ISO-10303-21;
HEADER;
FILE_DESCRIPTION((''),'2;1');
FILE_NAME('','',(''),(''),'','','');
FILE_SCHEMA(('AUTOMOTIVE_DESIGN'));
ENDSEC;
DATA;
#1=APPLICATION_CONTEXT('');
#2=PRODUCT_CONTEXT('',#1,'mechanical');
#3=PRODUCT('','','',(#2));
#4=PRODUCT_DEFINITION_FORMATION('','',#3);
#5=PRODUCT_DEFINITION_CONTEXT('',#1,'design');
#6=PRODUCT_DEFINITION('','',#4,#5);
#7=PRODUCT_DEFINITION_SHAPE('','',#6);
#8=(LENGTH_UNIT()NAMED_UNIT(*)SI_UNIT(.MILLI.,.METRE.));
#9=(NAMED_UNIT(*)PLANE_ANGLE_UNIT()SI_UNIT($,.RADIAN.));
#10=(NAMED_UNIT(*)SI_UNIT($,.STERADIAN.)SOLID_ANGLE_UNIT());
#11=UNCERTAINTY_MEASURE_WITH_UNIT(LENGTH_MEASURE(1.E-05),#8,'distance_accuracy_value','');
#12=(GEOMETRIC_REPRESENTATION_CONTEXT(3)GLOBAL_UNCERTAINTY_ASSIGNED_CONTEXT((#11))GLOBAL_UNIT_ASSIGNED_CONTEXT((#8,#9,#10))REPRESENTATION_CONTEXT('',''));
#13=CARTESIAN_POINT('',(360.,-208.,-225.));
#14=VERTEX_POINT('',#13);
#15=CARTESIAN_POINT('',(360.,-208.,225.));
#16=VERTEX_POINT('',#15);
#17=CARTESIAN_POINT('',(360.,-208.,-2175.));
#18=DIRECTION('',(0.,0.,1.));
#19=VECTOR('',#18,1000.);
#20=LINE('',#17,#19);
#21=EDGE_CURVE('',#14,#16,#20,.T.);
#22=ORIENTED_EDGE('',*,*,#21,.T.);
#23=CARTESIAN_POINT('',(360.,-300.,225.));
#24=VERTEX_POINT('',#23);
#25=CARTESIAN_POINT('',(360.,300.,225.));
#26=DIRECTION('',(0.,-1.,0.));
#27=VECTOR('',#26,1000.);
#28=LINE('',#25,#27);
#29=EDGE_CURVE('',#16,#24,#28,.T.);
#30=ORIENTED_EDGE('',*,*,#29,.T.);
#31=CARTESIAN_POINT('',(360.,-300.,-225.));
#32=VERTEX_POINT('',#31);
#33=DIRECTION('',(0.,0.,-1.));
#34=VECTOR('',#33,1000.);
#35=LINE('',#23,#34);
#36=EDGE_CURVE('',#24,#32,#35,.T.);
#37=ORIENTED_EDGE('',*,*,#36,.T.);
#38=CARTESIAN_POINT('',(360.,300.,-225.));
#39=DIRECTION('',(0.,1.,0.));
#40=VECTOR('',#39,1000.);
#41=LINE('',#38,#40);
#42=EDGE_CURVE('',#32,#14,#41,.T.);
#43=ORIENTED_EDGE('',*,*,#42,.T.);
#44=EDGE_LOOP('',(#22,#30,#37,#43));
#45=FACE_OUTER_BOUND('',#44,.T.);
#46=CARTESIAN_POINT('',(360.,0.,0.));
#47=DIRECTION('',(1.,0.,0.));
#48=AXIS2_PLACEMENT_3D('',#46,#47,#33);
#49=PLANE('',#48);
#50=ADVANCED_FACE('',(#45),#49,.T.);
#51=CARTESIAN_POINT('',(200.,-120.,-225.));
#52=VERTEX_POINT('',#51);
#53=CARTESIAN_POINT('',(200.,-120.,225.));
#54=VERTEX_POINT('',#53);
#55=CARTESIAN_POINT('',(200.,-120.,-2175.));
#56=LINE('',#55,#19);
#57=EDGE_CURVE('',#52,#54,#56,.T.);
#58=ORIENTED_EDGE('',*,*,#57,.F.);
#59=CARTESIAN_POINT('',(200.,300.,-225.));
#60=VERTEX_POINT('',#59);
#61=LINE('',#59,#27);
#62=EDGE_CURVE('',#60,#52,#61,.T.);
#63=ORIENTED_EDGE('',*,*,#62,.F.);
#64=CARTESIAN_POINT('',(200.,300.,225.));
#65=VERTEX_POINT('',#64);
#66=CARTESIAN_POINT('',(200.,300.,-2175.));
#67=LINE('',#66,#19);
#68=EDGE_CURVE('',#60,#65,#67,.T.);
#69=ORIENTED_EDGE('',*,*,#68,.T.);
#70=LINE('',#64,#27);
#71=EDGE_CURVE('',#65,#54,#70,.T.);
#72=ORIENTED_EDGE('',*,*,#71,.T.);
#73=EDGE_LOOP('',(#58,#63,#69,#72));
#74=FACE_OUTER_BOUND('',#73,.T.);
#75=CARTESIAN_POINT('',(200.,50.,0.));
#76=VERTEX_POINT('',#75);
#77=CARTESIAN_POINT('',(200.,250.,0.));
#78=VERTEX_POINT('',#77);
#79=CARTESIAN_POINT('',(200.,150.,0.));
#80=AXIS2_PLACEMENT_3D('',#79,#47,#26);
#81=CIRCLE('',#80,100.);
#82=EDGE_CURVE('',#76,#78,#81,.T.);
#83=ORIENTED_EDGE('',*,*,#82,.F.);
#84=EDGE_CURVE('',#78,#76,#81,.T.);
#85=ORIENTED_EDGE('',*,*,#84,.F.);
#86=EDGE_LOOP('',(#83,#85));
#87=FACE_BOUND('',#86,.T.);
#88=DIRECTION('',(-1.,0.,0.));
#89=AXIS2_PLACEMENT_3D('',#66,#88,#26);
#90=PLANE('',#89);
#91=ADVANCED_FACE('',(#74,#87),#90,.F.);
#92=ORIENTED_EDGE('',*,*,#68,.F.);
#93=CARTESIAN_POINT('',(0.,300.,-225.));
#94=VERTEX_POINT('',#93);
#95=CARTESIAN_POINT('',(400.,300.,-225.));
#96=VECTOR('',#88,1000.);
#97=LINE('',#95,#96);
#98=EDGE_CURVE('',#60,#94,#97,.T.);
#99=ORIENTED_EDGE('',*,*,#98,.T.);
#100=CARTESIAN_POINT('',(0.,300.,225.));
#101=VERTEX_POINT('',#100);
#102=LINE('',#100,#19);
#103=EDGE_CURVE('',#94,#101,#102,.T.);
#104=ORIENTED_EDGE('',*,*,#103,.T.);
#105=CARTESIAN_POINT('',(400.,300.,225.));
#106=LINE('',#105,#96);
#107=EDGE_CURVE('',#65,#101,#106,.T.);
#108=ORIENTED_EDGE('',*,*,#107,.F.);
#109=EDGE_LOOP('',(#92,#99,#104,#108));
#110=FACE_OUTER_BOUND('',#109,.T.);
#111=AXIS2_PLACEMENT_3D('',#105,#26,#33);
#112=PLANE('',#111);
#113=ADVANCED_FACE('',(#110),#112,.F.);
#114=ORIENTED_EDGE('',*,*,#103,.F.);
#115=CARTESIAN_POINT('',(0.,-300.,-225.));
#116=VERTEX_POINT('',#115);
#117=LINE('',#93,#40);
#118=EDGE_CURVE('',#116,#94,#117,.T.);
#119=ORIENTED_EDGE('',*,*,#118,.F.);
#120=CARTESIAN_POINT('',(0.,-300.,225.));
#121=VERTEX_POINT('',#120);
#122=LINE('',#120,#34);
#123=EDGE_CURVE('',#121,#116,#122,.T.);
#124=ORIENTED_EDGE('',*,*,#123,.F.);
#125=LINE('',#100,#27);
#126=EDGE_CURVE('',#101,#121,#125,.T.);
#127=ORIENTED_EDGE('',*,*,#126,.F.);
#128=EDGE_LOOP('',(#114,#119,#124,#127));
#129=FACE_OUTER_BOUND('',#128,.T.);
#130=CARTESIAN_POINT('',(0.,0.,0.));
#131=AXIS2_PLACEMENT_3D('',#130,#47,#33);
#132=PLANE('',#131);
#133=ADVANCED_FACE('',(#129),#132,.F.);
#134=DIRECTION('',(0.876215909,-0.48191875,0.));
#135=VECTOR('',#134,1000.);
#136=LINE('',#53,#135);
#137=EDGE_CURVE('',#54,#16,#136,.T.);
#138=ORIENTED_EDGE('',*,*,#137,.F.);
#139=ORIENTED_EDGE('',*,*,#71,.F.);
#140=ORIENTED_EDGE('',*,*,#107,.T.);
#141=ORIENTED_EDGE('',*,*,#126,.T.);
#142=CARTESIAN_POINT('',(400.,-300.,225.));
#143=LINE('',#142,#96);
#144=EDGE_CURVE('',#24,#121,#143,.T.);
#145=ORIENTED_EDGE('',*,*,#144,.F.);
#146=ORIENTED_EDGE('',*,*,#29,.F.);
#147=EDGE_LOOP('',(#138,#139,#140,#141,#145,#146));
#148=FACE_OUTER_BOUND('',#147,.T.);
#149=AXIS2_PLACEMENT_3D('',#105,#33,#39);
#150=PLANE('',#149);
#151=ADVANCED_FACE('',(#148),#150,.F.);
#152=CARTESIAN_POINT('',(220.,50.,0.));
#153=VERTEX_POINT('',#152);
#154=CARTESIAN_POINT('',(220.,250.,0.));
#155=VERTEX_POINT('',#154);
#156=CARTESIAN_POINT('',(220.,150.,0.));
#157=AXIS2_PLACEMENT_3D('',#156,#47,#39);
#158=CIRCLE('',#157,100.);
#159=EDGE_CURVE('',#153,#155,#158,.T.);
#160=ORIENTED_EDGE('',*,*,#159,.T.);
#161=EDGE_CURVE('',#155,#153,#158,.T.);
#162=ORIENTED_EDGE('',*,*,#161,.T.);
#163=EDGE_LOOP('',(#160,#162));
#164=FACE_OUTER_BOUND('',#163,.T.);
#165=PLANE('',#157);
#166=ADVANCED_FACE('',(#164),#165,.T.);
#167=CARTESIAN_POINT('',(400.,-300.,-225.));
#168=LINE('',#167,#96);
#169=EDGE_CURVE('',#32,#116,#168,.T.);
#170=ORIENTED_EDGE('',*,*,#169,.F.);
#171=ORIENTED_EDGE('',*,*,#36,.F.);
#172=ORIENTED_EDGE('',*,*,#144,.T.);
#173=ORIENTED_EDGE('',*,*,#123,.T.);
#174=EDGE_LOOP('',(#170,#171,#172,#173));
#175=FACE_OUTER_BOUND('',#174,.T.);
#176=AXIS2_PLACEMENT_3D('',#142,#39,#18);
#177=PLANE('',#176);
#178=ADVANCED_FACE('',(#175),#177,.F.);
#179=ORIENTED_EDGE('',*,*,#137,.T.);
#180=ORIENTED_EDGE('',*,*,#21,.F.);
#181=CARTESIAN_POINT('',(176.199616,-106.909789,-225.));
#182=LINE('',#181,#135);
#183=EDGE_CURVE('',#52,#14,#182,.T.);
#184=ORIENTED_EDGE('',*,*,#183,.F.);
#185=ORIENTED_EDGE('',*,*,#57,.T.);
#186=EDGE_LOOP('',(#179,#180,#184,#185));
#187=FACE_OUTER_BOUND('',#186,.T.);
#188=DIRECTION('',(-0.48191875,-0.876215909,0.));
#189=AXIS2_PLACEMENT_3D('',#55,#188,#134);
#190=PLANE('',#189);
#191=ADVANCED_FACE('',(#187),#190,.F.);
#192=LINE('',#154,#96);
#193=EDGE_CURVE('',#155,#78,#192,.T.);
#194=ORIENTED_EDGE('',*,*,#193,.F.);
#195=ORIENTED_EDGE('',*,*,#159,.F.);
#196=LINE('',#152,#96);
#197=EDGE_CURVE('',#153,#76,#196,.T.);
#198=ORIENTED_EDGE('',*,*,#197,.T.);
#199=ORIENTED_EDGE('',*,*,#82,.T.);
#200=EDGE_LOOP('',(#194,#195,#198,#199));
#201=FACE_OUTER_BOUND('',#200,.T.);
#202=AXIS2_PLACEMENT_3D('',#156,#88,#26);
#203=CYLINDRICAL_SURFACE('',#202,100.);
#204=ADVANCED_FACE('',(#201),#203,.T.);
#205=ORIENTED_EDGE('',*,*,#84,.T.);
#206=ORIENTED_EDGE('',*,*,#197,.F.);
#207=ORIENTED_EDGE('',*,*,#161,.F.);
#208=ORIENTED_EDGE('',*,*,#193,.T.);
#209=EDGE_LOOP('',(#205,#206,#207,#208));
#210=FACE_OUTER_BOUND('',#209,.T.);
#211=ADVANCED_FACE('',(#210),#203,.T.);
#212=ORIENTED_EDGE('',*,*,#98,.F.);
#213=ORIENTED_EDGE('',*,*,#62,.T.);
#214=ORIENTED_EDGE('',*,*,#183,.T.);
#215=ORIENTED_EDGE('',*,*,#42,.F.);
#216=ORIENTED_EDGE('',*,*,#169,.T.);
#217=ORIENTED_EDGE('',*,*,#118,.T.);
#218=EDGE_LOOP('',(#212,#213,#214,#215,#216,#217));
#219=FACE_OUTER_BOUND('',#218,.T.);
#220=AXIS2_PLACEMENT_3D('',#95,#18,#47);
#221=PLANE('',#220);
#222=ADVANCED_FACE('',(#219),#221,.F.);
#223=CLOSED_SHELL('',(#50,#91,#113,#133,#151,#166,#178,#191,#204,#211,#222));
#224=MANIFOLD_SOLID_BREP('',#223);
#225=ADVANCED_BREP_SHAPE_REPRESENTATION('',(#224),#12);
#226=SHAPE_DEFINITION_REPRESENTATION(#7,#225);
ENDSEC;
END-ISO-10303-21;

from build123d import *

# Parameters (mm, degrees)
SKETCH1_W           = 450
SKETCH1_H           = 600
BOSS_EXTRUDE1_DEPTH = 400
CUT_EXTRUDE1_DEPTH  = 2400
SKETCH4_W           = 648.804514889
SKETCH4_H           = 183.272574448
CUT_EXTRUDE2_DEPTH  = 40
SKETCH5_R           = 100
BOSS_EXTRUDE2_DEPTH = 20


with BuildPart() as part:
    # Sketch1 → Boss-Extrude1 (new body)
    with BuildSketch(Plane(origin=(0, 0, 0), x_dir=(0, 0, -1), z_dir=(1, 0, 0))):
        Rectangle(SKETCH1_W, SKETCH1_H)
    extrude(amount=BOSS_EXTRUDE1_DEPTH)

    # Sketch2 → Cut-Extrude1 (cut)
    with BuildSketch(Plane.XY.offset(225)):
        Polygon((200, 300), (200, -120), (400, -230), (400, 300), align=None)
    extrude(amount=-CUT_EXTRUDE1_DEPTH, mode=Mode.SUBTRACT)

    # Sketch4 → Cut-Extrude2 (cut)
    with BuildSketch(Plane(origin=(400, 0, 0), x_dir=(0, 0, -1), z_dir=(1, 0, 0))):
        with Locations((-2.450168107, -263.148054755)):
            Rectangle(SKETCH4_W, SKETCH4_H)
    extrude(amount=-CUT_EXTRUDE2_DEPTH, mode=Mode.SUBTRACT)

    # Sketch5 → Boss-Extrude2 (add)
    with BuildSketch(Plane(origin=(200, 0, 0), x_dir=(0, 0, -1), z_dir=(1, 0, 0))):
        with Locations(Location((0, 150, 0), (0, 0, 270))):
            Circle(SKETCH5_R)
    extrude(amount=BOSS_EXTRUDE2_DEPTH)


solid = part.part
